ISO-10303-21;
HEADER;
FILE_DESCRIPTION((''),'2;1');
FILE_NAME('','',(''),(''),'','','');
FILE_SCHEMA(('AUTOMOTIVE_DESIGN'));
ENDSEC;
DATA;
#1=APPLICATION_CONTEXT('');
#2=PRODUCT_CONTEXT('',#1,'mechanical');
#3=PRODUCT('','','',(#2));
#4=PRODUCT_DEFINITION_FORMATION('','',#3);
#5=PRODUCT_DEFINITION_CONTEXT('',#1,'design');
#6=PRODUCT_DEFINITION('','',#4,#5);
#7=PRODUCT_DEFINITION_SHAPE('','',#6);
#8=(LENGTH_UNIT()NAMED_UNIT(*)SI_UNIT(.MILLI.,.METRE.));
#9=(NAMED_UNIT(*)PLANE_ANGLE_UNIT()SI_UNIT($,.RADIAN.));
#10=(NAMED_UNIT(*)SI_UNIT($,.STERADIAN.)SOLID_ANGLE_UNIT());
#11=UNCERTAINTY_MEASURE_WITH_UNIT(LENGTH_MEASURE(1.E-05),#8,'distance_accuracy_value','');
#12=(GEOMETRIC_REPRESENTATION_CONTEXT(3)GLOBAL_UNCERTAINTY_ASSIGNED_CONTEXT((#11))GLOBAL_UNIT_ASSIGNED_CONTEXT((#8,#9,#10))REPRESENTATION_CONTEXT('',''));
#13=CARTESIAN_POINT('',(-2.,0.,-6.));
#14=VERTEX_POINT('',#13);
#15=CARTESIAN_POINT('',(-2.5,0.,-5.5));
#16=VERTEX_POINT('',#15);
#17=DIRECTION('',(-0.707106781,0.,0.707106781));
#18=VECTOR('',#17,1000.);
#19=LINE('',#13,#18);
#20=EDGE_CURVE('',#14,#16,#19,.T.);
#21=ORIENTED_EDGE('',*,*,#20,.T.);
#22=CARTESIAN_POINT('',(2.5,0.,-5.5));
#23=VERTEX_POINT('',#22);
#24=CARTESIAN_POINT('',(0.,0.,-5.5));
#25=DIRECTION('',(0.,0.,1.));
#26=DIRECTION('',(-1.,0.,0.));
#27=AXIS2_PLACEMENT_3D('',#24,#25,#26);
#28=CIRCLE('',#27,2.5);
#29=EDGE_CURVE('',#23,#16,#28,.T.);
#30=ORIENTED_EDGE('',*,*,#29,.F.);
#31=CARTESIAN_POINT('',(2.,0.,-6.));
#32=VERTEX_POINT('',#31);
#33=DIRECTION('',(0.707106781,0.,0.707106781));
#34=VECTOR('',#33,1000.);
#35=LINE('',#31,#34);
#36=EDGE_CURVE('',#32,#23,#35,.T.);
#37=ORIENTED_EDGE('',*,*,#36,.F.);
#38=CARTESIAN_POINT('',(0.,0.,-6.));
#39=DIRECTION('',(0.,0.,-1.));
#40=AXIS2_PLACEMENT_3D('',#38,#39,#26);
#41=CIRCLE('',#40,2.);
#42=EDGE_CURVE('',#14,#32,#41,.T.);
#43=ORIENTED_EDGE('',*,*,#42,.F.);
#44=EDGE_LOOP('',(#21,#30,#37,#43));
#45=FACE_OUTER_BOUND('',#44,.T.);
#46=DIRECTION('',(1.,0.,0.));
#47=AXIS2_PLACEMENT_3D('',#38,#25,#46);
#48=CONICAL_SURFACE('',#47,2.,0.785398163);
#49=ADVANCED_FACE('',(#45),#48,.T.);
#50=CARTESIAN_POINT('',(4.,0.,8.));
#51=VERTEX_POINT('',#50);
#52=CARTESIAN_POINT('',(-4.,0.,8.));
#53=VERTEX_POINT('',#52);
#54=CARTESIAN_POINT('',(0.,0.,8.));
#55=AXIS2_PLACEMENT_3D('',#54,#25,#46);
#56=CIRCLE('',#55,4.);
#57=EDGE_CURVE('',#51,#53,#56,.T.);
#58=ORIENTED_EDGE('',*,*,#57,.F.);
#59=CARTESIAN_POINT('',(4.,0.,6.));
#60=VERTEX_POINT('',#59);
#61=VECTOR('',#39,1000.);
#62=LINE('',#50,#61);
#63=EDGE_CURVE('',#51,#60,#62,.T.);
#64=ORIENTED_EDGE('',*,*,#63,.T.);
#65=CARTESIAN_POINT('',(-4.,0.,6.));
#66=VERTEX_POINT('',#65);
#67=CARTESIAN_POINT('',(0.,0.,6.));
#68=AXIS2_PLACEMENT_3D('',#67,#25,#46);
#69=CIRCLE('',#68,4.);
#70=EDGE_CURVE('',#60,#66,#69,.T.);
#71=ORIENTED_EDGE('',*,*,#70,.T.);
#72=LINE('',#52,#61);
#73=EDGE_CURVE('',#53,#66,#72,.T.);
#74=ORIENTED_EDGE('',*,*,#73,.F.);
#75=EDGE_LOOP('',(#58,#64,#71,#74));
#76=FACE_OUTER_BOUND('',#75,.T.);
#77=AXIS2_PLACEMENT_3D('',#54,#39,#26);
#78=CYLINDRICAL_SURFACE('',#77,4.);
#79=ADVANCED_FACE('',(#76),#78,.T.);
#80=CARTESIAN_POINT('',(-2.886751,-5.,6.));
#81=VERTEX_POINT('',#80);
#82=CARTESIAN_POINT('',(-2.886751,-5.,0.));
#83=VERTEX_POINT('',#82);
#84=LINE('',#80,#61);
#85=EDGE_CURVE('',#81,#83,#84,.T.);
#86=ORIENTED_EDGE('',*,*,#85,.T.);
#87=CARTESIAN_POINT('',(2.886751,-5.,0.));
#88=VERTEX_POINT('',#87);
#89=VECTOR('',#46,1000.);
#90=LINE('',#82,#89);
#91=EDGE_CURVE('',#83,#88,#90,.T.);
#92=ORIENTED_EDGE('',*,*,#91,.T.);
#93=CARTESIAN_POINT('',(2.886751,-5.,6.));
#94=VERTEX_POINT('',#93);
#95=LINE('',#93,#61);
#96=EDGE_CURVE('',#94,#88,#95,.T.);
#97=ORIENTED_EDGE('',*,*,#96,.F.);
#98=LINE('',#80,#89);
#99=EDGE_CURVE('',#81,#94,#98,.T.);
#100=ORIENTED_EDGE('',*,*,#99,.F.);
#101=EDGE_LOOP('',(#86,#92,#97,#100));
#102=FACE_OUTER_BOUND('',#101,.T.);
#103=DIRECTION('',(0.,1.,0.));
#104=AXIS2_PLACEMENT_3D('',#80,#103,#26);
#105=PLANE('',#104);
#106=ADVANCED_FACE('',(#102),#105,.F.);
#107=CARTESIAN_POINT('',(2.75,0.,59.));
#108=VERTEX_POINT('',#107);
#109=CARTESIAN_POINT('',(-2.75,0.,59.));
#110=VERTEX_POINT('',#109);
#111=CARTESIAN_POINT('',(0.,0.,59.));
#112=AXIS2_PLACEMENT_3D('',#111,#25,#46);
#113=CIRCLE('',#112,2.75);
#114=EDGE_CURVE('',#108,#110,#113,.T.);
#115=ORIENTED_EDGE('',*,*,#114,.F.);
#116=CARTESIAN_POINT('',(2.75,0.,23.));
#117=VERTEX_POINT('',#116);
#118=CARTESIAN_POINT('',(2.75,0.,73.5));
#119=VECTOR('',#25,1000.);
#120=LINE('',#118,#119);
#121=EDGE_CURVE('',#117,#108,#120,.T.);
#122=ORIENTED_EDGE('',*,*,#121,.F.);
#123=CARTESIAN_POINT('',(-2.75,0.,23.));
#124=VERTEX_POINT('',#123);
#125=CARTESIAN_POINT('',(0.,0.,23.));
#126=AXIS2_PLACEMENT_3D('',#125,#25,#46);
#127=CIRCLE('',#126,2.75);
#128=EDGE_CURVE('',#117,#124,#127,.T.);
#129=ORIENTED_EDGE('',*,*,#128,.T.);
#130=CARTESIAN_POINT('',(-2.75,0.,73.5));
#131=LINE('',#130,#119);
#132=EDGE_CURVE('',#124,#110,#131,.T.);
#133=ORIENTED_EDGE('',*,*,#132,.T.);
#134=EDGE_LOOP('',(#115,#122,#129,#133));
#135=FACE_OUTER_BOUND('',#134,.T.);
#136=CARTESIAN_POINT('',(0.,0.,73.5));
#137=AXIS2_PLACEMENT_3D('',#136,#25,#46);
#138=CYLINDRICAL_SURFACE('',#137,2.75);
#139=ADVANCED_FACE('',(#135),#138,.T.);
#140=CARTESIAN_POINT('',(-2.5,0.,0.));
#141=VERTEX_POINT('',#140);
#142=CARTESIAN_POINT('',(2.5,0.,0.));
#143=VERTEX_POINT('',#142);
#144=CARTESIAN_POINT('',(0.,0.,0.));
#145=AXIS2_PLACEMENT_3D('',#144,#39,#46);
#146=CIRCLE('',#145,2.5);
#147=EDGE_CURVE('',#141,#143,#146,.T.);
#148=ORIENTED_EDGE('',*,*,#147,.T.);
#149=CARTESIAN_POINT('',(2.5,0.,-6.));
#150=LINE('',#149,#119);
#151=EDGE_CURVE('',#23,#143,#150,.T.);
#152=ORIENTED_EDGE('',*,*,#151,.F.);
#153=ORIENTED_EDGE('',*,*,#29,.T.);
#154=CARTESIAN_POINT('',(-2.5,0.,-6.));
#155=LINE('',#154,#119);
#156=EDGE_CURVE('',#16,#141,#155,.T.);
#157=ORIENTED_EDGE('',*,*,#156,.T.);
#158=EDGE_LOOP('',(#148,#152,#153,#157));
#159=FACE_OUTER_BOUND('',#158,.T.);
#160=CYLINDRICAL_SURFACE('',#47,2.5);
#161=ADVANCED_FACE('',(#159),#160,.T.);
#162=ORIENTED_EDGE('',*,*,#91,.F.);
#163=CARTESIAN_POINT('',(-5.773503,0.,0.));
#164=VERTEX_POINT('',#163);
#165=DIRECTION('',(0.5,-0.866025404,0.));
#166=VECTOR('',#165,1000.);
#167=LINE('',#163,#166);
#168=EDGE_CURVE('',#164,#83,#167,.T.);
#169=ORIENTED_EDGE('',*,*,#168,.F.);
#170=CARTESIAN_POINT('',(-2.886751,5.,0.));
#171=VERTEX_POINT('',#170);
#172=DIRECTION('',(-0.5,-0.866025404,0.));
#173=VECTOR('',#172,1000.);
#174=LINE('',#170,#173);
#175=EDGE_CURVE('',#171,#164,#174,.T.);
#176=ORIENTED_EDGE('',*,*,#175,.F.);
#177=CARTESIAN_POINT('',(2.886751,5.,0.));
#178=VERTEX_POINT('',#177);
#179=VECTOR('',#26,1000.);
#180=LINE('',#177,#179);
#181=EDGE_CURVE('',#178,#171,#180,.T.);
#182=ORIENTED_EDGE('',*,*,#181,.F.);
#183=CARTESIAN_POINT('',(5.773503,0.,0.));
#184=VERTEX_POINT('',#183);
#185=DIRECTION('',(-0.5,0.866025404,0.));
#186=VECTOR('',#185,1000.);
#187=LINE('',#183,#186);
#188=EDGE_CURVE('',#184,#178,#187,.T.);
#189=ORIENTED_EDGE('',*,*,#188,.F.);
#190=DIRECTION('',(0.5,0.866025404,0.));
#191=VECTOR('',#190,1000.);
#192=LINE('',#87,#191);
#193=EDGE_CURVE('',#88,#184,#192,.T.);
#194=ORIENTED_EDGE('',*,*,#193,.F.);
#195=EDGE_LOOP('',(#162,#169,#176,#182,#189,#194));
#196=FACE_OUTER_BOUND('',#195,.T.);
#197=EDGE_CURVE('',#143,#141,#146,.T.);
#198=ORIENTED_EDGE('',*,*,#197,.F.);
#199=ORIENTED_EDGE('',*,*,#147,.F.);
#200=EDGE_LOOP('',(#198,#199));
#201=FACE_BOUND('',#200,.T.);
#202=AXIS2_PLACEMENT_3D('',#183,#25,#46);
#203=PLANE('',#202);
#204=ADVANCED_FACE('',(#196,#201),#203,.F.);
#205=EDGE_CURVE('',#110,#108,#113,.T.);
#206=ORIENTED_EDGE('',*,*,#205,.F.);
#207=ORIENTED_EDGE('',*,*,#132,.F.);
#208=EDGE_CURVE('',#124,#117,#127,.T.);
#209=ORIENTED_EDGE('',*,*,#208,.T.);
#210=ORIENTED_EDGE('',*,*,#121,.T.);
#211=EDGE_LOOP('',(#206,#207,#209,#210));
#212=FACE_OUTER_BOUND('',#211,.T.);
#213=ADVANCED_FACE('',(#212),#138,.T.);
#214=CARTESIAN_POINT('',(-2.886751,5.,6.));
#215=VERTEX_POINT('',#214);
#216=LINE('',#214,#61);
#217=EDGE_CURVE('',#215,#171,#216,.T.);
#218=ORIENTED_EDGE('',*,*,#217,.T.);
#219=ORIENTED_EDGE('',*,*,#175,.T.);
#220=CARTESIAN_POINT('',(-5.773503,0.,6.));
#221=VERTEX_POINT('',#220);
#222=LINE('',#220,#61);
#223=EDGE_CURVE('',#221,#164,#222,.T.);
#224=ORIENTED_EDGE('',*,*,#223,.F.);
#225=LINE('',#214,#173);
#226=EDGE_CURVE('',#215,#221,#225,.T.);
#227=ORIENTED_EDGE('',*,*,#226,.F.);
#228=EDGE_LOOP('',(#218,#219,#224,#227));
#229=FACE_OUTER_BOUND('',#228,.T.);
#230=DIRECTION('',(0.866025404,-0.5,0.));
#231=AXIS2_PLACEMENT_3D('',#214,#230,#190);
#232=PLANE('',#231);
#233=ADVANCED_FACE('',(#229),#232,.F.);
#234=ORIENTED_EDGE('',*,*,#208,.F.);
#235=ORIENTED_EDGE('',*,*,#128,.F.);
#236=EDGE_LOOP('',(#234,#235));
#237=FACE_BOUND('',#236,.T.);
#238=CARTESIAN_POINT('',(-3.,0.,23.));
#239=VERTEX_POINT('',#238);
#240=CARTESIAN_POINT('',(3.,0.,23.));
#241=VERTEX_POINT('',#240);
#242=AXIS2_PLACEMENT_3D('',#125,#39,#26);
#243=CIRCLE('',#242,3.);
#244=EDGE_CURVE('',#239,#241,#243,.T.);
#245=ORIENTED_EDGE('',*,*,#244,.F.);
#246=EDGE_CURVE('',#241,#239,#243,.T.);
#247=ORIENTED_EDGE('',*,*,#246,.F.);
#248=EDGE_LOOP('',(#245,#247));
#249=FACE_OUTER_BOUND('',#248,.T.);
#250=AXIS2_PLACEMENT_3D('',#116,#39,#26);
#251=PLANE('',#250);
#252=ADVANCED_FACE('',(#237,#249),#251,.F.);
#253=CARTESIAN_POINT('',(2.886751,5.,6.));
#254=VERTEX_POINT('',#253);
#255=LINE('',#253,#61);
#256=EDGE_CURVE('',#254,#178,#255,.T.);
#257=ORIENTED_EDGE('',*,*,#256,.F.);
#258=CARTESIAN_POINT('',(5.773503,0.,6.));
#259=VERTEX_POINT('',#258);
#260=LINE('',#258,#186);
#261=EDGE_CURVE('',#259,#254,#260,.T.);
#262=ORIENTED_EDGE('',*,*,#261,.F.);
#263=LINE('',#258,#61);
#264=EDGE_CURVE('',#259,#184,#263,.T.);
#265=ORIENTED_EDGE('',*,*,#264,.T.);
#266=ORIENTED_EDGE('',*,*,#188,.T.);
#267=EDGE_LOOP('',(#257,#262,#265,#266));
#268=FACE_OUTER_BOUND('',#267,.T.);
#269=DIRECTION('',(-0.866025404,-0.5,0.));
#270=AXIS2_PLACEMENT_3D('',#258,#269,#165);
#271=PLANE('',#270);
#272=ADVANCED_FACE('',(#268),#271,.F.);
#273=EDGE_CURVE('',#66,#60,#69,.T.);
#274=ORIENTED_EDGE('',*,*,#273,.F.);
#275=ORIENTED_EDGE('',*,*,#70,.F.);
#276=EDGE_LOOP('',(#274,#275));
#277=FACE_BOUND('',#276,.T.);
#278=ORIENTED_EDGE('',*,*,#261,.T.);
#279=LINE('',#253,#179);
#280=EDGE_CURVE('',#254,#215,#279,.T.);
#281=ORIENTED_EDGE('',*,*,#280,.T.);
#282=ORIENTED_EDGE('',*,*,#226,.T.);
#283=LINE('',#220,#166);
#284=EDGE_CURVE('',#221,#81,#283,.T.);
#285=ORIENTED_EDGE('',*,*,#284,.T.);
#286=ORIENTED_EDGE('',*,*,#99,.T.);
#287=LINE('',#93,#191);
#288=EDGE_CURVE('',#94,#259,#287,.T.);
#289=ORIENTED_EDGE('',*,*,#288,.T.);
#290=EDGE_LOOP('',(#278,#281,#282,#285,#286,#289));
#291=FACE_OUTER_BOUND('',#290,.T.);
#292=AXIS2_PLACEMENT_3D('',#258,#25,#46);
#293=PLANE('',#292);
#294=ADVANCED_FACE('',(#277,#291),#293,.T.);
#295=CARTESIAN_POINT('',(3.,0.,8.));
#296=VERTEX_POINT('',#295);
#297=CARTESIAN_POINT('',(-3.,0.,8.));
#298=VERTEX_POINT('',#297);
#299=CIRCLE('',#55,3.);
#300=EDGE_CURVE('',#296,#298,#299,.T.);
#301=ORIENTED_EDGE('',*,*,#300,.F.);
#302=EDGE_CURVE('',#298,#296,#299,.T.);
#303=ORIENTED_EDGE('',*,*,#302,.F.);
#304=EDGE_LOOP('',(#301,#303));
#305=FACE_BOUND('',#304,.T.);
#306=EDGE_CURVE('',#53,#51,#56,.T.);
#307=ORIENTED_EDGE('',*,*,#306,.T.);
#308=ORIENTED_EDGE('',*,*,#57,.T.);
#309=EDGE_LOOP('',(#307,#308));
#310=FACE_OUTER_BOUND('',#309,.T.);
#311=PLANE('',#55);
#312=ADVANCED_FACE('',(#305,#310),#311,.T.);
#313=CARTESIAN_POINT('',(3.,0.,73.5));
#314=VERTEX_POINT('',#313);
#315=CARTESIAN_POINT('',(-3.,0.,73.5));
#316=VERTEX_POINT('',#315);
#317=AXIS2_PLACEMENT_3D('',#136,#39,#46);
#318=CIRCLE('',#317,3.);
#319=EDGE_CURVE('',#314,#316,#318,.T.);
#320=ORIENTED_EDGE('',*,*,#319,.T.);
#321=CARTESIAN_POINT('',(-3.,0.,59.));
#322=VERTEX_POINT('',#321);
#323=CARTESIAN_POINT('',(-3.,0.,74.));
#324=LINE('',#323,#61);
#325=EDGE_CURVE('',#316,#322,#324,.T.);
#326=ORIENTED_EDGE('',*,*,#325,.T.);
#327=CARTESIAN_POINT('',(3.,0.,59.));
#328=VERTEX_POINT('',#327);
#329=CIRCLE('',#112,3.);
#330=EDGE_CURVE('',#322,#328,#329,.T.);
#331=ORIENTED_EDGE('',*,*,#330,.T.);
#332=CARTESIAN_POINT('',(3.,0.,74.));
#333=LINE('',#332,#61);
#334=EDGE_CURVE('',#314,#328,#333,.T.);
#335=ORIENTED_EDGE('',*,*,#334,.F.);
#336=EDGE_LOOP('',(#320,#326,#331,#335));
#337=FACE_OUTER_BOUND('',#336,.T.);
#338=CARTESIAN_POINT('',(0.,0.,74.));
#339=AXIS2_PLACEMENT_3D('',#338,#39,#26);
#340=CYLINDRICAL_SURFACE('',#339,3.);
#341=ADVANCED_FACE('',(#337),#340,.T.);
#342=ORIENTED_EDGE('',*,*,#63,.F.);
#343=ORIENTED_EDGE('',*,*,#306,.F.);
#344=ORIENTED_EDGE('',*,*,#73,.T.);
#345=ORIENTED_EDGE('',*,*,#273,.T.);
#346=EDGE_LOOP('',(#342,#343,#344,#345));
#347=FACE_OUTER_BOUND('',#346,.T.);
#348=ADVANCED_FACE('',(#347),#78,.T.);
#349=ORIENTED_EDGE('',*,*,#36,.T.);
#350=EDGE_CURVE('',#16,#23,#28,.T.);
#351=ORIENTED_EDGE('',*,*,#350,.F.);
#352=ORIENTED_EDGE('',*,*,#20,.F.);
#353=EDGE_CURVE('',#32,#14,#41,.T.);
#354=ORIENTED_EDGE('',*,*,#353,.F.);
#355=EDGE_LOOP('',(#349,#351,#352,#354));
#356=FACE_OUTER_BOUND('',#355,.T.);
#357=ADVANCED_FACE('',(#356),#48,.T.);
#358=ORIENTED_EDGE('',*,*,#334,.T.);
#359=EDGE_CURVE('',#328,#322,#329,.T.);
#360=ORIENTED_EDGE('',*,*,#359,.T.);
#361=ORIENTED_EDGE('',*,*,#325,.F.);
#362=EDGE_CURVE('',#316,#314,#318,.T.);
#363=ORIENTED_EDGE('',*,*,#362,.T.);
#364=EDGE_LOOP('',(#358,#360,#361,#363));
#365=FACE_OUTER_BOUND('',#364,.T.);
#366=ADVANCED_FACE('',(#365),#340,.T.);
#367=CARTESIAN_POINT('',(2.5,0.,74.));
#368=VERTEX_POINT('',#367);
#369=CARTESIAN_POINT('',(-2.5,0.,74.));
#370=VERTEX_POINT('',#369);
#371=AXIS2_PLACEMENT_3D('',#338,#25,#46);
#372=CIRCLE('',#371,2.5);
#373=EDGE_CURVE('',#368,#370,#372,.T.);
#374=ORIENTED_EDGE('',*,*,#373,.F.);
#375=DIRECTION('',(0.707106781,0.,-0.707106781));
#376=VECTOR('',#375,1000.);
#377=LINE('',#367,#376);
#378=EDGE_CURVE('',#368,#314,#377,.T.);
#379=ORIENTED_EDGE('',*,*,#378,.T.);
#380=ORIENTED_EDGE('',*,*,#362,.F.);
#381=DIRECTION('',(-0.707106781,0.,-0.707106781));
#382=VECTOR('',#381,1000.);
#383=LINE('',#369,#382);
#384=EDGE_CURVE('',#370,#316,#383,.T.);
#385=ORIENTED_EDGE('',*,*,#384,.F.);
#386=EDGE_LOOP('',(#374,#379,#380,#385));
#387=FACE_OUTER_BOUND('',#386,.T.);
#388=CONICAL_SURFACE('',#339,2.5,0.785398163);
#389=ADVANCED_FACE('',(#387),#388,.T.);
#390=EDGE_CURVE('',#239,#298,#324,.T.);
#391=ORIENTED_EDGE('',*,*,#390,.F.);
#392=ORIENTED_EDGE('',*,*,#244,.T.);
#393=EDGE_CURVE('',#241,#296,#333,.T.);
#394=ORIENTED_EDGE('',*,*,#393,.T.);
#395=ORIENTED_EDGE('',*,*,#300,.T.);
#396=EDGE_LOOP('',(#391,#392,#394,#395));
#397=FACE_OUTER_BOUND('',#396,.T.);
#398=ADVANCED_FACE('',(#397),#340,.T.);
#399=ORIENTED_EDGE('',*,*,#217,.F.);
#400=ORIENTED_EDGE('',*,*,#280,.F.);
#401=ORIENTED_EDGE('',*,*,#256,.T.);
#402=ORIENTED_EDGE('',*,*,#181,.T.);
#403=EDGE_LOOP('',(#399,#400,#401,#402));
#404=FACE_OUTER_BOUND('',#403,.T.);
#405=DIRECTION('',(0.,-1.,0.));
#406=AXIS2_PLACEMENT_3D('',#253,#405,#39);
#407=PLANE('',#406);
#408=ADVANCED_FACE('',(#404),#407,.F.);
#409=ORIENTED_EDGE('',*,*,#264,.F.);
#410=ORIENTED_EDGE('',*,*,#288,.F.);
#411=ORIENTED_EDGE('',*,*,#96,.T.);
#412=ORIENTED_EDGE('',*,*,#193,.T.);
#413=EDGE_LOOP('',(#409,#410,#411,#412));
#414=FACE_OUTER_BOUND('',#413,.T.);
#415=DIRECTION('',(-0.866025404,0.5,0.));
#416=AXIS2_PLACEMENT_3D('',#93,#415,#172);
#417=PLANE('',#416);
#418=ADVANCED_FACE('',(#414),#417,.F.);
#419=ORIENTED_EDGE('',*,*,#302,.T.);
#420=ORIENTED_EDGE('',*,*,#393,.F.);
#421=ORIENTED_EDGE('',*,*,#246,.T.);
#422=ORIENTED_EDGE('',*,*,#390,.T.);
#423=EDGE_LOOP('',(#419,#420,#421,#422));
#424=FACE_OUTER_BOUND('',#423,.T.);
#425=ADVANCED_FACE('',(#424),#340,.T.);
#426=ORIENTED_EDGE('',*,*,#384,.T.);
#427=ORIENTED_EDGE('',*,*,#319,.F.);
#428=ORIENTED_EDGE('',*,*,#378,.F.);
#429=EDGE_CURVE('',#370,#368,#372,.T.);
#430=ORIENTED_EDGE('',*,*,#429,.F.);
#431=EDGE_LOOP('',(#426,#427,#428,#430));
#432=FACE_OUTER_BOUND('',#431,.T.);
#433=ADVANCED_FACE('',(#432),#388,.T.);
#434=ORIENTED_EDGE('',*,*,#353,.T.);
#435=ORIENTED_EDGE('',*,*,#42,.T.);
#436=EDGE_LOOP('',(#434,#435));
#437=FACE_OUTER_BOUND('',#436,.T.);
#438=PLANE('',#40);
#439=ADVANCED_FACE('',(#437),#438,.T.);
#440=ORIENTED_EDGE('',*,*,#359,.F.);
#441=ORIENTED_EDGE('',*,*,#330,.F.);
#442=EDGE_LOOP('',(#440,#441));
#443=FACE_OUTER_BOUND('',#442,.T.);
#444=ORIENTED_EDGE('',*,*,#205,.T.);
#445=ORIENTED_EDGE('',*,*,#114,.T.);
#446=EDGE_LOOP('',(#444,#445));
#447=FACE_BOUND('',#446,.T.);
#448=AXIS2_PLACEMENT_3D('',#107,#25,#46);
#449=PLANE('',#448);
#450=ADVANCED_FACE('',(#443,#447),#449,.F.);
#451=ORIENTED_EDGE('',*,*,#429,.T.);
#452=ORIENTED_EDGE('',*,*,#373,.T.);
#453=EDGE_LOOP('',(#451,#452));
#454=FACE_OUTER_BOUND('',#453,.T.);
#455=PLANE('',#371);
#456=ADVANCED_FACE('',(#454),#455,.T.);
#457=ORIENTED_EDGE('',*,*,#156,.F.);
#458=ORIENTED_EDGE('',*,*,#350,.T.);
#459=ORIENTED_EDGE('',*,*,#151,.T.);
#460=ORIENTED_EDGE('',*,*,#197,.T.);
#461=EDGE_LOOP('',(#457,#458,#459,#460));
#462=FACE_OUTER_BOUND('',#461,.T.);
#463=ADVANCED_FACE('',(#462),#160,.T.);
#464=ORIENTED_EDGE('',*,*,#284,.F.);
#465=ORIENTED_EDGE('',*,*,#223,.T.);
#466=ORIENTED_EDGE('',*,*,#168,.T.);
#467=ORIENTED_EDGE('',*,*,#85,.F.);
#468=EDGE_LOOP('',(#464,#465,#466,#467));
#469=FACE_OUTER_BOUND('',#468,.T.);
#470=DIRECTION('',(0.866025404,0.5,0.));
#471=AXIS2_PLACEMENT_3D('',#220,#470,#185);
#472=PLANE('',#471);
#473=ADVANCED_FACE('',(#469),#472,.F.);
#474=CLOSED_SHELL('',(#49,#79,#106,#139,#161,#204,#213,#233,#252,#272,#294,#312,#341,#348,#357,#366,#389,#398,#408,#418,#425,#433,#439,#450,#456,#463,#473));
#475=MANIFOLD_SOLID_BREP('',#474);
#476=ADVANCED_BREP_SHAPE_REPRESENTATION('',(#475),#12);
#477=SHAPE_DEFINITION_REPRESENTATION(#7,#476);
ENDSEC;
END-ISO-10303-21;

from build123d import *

# Parameters (mm, degrees)
BOSS_EXTRUDE1_DEPTH = 6
SKETCH2_R           = 2.5
BOSS_EXTRUDE2_DEPTH = 6
SKETCH3_R           = 4
BOSS_EXTRUDE3_DEPTH = 2
SKETCH4_R           = 3
BOSS_EXTRUDE4_DEPTH = 66
CHAMFER1_SIZE       = 0.5
SKETCH5_W           = 5
SKETCH5_H           = 36
CHAMFER2_SIZE       = 0.5


with BuildPart() as part:
    # Sketch1 → Boss-Extrude1 (new body)
    with BuildSketch(Plane.XY):
        Polygon((5.773502692, 0), (2.886751346, 5), (-2.886751346, 5), (-5.773502692, 0), (-2.886751346, -5), (2.886751346, -5), align=None)
    extrude(amount=BOSS_EXTRUDE1_DEPTH)

    # Sketch2 → Boss-Extrude2 (add)
    with BuildSketch(Plane(origin=(0, 0, 0), x_dir=(-1, 0, 0), z_dir=(0, 0, -1))):
        with Locations(Location((0, 0, 0), (0, 0, 180))):
            Circle(SKETCH2_R)
    extrude(amount=BOSS_EXTRUDE2_DEPTH)

    # Sketch3 → Boss-Extrude3 (add)
    with BuildSketch(Plane.XY.offset(6)):
        Circle(SKETCH3_R)
    extrude(amount=BOSS_EXTRUDE3_DEPTH)

    # Sketch4 → Boss-Extrude4 (add)
    with BuildSketch(Plane.XY.offset(8)):
        Circle(SKETCH4_R)
    extrude(amount=BOSS_EXTRUDE4_DEPTH)

    # Chamfer1
    chamfer1_edges = [part.edges().sort_by_distance(p)[0] for p in [
        (-3, 0, 74),
    ]]
    chamfer(chamfer1_edges, length=CHAMFER1_SIZE)

    # Sketch5 → Cut-Revolve1 (revolve, cut)
    with BuildSketch(Plane(origin=(0, 0, 0), x_dir=(1, 0, 0), z_dir=(0, 1, 0))):
        with Locations((5.25, -41)):
            Rectangle(SKETCH5_W, SKETCH5_H)
    revolve(axis=Axis((0, 0, 73.5), (0, 0, -1)), mode=Mode.SUBTRACT)

    # Chamfer2
    chamfer2_edges = [part.edges().sort_by_distance(p)[0] for p in [
        (-2.5, 0, -6),
    ]]
    chamfer(chamfer2_edges, length=CHAMFER2_SIZE)


solid = part.part
